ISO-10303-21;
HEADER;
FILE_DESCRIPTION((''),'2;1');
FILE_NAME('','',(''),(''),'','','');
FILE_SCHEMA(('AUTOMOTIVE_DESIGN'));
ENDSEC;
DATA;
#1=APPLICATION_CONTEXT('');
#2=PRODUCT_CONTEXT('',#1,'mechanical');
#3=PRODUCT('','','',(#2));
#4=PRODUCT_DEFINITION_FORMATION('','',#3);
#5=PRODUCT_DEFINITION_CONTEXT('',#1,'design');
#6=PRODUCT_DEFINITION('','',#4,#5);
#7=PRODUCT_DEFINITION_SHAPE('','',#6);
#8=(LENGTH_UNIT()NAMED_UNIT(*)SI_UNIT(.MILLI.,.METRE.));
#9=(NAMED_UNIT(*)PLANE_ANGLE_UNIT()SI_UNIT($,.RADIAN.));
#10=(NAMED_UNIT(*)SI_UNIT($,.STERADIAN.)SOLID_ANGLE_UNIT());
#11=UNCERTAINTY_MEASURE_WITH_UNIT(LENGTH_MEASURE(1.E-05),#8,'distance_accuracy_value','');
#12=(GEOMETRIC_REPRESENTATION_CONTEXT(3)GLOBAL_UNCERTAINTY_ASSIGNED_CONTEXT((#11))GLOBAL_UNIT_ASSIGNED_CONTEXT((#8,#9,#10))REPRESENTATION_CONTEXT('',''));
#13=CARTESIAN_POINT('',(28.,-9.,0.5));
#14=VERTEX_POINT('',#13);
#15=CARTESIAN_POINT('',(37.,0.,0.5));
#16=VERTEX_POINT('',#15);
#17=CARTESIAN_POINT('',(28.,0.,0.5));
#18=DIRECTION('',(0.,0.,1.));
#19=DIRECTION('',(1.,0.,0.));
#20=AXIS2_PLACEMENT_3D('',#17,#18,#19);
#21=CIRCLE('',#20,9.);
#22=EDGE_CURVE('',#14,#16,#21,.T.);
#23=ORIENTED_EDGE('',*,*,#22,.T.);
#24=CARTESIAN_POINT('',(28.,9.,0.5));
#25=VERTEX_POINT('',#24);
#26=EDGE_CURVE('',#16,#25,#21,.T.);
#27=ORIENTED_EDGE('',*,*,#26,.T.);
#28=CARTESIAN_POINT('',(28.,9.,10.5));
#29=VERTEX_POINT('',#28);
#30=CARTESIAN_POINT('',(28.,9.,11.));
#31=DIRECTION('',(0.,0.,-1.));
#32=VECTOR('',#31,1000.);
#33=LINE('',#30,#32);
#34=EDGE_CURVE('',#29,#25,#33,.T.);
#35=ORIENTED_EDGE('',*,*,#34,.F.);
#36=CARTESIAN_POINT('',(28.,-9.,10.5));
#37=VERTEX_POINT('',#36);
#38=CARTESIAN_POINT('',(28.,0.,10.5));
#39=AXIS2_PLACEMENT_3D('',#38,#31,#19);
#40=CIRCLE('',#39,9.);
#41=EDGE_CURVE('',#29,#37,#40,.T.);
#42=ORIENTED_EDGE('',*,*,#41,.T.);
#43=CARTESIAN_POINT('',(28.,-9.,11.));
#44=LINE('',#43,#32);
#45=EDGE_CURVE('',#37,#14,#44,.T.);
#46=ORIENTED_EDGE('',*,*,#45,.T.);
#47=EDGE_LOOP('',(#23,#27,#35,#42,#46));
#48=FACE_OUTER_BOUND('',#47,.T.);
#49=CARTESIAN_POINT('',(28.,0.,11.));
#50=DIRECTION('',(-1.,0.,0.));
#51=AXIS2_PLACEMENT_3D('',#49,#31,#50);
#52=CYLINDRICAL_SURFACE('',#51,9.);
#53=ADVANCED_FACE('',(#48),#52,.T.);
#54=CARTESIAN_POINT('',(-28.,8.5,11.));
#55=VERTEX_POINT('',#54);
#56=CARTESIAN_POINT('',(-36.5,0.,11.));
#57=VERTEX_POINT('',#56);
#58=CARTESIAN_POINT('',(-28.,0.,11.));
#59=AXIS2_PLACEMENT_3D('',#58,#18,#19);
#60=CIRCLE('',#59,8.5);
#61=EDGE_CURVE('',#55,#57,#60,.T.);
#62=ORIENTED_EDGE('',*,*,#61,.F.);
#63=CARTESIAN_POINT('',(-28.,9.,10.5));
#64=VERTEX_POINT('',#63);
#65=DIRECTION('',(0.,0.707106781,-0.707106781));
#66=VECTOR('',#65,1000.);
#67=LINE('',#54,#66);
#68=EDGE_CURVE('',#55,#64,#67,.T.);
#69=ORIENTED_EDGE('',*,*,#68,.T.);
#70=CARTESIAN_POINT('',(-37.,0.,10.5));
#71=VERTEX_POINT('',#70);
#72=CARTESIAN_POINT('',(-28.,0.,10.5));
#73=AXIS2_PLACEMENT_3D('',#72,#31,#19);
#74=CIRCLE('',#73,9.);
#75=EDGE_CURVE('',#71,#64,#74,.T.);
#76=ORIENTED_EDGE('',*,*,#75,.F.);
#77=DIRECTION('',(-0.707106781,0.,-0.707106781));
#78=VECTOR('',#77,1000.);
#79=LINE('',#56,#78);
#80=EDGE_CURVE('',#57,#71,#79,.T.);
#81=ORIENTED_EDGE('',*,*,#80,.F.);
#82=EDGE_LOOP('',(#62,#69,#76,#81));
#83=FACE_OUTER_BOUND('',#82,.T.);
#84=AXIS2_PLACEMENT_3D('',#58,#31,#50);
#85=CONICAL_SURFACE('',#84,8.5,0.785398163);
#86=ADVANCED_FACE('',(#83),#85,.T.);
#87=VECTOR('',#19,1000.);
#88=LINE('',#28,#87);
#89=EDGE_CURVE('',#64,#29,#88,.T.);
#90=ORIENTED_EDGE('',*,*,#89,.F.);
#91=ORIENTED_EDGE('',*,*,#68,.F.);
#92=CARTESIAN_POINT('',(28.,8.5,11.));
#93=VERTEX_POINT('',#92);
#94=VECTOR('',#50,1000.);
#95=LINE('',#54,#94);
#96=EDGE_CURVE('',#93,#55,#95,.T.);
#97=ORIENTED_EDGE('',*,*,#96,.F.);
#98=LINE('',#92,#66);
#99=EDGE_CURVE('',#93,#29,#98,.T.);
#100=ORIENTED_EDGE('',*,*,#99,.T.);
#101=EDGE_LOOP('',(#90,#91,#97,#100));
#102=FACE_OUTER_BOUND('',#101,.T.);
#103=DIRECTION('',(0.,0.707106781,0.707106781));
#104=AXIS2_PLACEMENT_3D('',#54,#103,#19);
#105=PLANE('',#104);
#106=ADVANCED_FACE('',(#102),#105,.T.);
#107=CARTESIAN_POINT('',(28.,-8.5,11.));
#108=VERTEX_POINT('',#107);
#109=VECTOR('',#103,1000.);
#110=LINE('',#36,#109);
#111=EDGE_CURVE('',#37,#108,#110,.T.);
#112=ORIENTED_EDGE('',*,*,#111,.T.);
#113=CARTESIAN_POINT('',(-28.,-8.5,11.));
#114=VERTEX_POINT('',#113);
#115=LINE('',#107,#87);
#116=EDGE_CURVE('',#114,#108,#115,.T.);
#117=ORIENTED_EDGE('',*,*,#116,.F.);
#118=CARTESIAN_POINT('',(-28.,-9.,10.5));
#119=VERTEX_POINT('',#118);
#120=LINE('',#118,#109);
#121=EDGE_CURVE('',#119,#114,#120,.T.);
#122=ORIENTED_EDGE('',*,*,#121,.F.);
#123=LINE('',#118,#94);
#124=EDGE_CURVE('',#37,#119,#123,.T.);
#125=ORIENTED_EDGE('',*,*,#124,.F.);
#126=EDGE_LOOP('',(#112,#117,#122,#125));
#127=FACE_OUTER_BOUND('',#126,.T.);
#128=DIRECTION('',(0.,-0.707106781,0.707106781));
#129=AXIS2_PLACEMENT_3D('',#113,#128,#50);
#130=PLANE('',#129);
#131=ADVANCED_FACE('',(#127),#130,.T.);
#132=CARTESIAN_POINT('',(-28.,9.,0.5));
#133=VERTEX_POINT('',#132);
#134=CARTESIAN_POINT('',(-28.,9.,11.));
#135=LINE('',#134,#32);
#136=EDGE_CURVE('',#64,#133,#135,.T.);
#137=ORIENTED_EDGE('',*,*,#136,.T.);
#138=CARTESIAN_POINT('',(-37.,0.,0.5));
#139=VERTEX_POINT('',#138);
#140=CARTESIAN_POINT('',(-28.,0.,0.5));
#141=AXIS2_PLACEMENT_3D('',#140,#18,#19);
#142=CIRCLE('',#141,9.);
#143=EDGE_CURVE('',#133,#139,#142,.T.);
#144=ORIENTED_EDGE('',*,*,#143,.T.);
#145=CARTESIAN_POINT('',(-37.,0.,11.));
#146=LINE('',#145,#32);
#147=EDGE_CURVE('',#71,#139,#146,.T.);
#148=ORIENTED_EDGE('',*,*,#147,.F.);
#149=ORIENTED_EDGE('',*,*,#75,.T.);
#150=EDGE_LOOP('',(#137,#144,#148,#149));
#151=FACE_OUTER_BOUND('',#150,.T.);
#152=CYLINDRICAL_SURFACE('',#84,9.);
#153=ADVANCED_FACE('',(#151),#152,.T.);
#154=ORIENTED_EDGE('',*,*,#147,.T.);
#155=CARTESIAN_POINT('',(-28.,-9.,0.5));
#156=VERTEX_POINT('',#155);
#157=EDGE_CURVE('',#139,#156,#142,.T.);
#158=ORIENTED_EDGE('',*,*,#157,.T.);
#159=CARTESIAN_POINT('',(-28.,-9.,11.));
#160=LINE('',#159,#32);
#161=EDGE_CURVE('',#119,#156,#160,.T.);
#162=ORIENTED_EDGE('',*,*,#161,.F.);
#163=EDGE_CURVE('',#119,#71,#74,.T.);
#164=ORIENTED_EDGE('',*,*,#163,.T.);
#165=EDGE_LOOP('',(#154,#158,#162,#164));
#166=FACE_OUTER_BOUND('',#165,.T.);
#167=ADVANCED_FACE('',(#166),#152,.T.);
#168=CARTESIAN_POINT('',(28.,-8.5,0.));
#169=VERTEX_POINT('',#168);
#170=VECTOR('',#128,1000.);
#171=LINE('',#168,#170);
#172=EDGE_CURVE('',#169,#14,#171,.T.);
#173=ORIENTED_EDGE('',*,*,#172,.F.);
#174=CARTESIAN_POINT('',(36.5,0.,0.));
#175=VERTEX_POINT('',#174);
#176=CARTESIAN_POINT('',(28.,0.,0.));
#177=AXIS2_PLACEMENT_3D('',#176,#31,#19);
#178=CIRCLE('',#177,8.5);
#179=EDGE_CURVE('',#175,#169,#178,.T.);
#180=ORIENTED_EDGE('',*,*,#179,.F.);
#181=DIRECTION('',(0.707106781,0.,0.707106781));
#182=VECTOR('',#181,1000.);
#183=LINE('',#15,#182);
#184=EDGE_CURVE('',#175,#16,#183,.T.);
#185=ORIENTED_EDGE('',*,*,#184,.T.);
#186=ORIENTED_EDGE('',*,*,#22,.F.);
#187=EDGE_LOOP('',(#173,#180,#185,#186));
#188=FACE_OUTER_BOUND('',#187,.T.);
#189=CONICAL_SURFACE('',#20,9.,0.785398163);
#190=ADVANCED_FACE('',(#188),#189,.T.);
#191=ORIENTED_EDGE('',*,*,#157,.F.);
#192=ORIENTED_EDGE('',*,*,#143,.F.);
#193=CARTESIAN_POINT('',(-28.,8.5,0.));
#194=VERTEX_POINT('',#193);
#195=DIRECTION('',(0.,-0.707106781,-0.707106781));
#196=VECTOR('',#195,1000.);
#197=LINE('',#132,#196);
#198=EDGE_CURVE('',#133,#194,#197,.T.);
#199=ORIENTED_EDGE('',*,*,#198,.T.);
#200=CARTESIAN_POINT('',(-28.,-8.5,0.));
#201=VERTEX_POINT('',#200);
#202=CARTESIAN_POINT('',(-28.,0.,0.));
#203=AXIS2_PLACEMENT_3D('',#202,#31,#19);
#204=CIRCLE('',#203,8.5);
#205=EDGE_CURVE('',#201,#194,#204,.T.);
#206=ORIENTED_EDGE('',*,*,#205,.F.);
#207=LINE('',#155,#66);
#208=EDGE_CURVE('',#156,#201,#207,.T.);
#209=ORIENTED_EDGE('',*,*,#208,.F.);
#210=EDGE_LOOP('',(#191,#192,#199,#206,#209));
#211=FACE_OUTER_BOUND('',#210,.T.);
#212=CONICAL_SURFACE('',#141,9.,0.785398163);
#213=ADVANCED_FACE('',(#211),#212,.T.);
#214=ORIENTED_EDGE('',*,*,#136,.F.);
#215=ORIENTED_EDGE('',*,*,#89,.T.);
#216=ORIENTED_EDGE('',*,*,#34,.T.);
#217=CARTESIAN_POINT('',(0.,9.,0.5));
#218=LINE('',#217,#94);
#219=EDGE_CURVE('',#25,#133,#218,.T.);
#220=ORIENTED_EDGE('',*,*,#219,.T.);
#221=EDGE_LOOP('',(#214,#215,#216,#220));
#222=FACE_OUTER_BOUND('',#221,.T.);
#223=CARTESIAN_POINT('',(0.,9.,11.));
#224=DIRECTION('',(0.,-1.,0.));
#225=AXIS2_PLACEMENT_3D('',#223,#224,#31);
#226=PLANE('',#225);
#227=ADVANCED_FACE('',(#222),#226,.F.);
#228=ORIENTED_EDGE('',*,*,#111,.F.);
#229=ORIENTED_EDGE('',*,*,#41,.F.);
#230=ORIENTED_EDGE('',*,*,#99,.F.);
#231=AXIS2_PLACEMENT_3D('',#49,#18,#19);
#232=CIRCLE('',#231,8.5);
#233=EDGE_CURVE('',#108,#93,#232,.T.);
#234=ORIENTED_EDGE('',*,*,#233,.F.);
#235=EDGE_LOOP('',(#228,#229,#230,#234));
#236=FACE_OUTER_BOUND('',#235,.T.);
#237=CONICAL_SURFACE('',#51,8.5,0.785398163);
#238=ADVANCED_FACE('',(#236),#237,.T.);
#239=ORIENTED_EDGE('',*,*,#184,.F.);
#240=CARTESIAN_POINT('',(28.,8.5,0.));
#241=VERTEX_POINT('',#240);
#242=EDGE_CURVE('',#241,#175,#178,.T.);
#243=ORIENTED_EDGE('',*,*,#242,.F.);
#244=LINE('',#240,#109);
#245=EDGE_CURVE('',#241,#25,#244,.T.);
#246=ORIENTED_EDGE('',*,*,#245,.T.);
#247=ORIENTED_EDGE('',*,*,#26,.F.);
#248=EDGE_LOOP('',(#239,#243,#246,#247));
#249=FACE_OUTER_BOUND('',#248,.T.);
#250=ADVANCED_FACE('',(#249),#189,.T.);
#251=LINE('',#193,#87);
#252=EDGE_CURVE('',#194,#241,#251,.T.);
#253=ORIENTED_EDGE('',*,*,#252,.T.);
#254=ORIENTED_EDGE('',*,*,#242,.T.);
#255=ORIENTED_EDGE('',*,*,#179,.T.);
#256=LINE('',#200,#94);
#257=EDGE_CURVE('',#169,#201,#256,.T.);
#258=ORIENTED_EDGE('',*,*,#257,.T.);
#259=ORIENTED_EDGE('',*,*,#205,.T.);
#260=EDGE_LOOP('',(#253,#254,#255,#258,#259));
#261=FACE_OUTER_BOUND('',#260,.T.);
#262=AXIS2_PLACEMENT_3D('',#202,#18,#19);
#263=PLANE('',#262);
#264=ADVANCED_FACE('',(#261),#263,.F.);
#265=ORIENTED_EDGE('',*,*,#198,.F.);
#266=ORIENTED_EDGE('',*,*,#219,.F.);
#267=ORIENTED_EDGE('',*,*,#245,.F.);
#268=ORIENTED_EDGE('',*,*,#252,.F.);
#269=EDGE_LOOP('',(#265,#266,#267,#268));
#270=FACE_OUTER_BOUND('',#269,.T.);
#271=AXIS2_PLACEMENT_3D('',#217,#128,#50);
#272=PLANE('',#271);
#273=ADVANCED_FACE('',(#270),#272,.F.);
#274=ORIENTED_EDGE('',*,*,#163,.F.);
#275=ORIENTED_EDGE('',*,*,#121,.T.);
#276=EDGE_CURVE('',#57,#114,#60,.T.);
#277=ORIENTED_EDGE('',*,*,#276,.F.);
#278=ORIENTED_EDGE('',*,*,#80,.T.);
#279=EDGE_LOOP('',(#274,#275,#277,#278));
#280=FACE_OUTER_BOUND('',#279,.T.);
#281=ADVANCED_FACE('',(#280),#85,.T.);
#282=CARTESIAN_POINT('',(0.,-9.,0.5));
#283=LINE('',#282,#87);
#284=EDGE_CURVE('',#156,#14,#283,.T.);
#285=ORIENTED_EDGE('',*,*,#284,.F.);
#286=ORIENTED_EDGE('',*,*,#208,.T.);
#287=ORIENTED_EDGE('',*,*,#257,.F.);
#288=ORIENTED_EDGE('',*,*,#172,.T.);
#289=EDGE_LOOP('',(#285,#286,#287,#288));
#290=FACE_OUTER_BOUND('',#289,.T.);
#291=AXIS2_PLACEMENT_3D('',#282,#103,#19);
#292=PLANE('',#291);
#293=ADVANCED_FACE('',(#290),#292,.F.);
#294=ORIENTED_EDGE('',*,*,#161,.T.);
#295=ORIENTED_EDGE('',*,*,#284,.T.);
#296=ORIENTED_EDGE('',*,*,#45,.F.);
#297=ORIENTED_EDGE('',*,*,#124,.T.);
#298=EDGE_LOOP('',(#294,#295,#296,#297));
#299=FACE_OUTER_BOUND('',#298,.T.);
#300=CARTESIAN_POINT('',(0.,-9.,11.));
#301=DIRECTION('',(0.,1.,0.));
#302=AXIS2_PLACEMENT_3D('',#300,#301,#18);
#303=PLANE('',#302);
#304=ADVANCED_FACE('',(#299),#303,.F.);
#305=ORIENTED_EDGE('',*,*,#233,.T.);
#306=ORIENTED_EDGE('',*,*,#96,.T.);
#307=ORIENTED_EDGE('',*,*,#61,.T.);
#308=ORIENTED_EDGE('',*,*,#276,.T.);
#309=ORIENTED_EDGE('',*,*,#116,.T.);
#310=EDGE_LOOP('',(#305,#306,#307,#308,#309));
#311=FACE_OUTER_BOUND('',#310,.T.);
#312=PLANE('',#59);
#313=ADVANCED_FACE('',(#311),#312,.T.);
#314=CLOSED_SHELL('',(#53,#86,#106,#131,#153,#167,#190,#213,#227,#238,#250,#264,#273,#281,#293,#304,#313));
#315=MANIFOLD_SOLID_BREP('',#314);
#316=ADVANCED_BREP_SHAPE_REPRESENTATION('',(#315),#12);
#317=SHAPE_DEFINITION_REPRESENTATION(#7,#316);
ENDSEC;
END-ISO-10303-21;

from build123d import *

# Parameters (mm, degrees)
BOSS_EXTRUDE1_DEPTH = 11
CHAMFER1_SIZE       = 0.5


with BuildPart() as part:
    # Sketch1 → Boss-Extrude1 (new body)
    with BuildSketch(Plane.XY):
        with BuildLine():
            Line((0, 9), (28, 9))
            ThreePointArc((28, 9), (37, 0), (28, -9))
            Line((28, -9), (0, -9))
            Line((0, -9), (-28, -9))
            ThreePointArc((-28, -9), (-37, 0), (-28, 9))
            Line((-28, 9), (0, 9))
        make_face()
    extrude(amount=BOSS_EXTRUDE1_DEPTH)

    # Chamfer1
    chamfer1_edges = [part.edges().sort_by_distance(p)[0] for p in [
        (0, -9, 11),
        (37, 0, 11),
        (0, 9, 11),
        (0, 9, 0),
        (37, 0, 0),
        (0, -9, 0),
        (-37, 0, 0),
        (-37, 0, 11),
    ]]
    chamfer(chamfer1_edges, length=CHAMFER1_SIZE)


solid = part.part
